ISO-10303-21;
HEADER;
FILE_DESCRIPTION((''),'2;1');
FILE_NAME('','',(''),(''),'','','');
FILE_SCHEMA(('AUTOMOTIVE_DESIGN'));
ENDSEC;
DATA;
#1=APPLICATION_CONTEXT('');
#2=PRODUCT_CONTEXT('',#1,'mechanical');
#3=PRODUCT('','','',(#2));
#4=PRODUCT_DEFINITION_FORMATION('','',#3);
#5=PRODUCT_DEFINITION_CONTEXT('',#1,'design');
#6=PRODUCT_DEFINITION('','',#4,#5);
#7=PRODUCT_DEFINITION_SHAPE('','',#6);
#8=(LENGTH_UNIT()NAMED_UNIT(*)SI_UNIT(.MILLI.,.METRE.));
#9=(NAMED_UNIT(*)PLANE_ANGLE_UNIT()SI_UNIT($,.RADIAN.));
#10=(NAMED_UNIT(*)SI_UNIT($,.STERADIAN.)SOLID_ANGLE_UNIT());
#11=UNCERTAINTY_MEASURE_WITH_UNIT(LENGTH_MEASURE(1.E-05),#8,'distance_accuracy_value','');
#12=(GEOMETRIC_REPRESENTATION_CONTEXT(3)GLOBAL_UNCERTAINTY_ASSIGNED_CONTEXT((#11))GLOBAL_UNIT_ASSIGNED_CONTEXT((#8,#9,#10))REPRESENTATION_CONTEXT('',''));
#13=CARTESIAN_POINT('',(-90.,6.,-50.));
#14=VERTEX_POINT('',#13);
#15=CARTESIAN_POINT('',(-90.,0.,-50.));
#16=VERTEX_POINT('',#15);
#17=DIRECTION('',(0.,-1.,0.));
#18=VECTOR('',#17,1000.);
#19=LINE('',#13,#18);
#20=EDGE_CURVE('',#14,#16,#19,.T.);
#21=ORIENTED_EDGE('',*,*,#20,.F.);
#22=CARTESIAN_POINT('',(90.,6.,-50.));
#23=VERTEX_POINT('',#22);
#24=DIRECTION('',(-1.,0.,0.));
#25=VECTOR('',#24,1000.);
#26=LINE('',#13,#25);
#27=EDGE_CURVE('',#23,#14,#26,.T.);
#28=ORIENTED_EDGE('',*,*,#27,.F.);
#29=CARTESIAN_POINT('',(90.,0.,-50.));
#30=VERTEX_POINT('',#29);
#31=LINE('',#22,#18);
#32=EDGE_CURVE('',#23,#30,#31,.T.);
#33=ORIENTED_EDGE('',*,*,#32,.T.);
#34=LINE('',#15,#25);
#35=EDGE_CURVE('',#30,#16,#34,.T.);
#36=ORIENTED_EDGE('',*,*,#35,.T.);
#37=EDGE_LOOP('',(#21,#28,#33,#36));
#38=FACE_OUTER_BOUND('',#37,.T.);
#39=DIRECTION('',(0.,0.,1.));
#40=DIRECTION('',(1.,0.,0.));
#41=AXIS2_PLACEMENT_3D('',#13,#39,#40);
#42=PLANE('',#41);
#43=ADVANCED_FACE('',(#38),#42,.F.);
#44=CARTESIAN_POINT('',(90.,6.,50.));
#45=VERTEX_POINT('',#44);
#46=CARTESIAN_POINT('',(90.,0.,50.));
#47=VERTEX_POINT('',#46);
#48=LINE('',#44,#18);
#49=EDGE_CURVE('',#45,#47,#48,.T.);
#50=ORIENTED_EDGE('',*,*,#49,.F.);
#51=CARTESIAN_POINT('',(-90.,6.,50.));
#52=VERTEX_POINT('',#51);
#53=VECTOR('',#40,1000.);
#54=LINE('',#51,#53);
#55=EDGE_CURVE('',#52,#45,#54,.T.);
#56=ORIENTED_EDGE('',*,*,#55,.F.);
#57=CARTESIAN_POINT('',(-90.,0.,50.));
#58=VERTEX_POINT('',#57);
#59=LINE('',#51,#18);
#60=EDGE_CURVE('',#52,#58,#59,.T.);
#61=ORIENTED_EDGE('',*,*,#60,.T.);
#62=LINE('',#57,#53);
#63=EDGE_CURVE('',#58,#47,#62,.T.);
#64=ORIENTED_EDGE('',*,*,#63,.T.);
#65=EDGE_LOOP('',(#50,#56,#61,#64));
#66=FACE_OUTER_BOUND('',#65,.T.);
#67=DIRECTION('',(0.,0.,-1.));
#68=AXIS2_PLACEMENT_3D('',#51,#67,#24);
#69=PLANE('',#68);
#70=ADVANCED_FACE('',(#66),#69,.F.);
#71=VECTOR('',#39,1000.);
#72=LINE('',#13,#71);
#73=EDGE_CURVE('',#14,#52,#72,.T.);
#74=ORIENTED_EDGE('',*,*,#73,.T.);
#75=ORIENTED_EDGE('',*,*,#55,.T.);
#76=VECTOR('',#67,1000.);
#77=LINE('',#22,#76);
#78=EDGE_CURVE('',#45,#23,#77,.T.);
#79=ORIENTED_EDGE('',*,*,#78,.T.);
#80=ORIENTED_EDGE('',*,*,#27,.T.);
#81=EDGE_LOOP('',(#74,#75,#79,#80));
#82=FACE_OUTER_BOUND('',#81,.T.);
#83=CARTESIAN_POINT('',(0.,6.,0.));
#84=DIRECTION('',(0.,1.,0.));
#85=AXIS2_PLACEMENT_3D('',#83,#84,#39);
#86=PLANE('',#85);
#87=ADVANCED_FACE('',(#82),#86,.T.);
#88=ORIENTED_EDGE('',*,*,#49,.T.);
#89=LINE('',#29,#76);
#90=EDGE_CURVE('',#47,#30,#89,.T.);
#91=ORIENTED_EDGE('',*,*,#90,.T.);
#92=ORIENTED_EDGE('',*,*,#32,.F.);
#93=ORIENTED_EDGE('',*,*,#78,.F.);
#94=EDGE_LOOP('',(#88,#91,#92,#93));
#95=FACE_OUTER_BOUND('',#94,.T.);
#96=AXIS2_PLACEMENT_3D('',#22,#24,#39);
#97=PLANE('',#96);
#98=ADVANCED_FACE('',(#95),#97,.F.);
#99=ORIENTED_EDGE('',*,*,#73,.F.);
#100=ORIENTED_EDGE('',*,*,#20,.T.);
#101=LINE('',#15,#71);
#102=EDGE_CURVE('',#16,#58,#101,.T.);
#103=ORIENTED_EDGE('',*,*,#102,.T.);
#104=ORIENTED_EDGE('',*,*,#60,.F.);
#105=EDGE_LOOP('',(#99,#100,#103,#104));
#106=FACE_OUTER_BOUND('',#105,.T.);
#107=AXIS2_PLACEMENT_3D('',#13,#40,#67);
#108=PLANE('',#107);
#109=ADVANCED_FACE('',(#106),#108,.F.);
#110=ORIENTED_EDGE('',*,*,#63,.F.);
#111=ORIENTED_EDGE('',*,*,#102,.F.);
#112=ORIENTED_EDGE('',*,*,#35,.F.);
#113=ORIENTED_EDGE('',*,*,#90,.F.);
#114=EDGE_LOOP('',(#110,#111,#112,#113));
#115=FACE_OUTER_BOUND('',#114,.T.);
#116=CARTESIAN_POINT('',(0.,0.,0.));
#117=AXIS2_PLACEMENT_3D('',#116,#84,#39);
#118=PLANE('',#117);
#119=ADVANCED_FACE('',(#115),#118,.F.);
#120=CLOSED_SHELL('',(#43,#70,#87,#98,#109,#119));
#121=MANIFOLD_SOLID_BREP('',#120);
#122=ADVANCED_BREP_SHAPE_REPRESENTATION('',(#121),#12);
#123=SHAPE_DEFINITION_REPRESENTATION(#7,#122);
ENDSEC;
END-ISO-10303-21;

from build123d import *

# Parameters (mm, degrees)
SKETCH1_W           = 180
SKETCH1_H           = 100
BOSS_EXTRUDE1_DEPTH = 6


with BuildPart() as part:
    # Sketch1 → Boss-Extrude1 (new body)
    with BuildSketch(Plane(origin=(0, 0, 0), x_dir=(1, 0, 0), z_dir=(0, 1, 0))):
        Rectangle(SKETCH1_W, SKETCH1_H)
    extrude(amount=BOSS_EXTRUDE1_DEPTH)


solid = part.part
